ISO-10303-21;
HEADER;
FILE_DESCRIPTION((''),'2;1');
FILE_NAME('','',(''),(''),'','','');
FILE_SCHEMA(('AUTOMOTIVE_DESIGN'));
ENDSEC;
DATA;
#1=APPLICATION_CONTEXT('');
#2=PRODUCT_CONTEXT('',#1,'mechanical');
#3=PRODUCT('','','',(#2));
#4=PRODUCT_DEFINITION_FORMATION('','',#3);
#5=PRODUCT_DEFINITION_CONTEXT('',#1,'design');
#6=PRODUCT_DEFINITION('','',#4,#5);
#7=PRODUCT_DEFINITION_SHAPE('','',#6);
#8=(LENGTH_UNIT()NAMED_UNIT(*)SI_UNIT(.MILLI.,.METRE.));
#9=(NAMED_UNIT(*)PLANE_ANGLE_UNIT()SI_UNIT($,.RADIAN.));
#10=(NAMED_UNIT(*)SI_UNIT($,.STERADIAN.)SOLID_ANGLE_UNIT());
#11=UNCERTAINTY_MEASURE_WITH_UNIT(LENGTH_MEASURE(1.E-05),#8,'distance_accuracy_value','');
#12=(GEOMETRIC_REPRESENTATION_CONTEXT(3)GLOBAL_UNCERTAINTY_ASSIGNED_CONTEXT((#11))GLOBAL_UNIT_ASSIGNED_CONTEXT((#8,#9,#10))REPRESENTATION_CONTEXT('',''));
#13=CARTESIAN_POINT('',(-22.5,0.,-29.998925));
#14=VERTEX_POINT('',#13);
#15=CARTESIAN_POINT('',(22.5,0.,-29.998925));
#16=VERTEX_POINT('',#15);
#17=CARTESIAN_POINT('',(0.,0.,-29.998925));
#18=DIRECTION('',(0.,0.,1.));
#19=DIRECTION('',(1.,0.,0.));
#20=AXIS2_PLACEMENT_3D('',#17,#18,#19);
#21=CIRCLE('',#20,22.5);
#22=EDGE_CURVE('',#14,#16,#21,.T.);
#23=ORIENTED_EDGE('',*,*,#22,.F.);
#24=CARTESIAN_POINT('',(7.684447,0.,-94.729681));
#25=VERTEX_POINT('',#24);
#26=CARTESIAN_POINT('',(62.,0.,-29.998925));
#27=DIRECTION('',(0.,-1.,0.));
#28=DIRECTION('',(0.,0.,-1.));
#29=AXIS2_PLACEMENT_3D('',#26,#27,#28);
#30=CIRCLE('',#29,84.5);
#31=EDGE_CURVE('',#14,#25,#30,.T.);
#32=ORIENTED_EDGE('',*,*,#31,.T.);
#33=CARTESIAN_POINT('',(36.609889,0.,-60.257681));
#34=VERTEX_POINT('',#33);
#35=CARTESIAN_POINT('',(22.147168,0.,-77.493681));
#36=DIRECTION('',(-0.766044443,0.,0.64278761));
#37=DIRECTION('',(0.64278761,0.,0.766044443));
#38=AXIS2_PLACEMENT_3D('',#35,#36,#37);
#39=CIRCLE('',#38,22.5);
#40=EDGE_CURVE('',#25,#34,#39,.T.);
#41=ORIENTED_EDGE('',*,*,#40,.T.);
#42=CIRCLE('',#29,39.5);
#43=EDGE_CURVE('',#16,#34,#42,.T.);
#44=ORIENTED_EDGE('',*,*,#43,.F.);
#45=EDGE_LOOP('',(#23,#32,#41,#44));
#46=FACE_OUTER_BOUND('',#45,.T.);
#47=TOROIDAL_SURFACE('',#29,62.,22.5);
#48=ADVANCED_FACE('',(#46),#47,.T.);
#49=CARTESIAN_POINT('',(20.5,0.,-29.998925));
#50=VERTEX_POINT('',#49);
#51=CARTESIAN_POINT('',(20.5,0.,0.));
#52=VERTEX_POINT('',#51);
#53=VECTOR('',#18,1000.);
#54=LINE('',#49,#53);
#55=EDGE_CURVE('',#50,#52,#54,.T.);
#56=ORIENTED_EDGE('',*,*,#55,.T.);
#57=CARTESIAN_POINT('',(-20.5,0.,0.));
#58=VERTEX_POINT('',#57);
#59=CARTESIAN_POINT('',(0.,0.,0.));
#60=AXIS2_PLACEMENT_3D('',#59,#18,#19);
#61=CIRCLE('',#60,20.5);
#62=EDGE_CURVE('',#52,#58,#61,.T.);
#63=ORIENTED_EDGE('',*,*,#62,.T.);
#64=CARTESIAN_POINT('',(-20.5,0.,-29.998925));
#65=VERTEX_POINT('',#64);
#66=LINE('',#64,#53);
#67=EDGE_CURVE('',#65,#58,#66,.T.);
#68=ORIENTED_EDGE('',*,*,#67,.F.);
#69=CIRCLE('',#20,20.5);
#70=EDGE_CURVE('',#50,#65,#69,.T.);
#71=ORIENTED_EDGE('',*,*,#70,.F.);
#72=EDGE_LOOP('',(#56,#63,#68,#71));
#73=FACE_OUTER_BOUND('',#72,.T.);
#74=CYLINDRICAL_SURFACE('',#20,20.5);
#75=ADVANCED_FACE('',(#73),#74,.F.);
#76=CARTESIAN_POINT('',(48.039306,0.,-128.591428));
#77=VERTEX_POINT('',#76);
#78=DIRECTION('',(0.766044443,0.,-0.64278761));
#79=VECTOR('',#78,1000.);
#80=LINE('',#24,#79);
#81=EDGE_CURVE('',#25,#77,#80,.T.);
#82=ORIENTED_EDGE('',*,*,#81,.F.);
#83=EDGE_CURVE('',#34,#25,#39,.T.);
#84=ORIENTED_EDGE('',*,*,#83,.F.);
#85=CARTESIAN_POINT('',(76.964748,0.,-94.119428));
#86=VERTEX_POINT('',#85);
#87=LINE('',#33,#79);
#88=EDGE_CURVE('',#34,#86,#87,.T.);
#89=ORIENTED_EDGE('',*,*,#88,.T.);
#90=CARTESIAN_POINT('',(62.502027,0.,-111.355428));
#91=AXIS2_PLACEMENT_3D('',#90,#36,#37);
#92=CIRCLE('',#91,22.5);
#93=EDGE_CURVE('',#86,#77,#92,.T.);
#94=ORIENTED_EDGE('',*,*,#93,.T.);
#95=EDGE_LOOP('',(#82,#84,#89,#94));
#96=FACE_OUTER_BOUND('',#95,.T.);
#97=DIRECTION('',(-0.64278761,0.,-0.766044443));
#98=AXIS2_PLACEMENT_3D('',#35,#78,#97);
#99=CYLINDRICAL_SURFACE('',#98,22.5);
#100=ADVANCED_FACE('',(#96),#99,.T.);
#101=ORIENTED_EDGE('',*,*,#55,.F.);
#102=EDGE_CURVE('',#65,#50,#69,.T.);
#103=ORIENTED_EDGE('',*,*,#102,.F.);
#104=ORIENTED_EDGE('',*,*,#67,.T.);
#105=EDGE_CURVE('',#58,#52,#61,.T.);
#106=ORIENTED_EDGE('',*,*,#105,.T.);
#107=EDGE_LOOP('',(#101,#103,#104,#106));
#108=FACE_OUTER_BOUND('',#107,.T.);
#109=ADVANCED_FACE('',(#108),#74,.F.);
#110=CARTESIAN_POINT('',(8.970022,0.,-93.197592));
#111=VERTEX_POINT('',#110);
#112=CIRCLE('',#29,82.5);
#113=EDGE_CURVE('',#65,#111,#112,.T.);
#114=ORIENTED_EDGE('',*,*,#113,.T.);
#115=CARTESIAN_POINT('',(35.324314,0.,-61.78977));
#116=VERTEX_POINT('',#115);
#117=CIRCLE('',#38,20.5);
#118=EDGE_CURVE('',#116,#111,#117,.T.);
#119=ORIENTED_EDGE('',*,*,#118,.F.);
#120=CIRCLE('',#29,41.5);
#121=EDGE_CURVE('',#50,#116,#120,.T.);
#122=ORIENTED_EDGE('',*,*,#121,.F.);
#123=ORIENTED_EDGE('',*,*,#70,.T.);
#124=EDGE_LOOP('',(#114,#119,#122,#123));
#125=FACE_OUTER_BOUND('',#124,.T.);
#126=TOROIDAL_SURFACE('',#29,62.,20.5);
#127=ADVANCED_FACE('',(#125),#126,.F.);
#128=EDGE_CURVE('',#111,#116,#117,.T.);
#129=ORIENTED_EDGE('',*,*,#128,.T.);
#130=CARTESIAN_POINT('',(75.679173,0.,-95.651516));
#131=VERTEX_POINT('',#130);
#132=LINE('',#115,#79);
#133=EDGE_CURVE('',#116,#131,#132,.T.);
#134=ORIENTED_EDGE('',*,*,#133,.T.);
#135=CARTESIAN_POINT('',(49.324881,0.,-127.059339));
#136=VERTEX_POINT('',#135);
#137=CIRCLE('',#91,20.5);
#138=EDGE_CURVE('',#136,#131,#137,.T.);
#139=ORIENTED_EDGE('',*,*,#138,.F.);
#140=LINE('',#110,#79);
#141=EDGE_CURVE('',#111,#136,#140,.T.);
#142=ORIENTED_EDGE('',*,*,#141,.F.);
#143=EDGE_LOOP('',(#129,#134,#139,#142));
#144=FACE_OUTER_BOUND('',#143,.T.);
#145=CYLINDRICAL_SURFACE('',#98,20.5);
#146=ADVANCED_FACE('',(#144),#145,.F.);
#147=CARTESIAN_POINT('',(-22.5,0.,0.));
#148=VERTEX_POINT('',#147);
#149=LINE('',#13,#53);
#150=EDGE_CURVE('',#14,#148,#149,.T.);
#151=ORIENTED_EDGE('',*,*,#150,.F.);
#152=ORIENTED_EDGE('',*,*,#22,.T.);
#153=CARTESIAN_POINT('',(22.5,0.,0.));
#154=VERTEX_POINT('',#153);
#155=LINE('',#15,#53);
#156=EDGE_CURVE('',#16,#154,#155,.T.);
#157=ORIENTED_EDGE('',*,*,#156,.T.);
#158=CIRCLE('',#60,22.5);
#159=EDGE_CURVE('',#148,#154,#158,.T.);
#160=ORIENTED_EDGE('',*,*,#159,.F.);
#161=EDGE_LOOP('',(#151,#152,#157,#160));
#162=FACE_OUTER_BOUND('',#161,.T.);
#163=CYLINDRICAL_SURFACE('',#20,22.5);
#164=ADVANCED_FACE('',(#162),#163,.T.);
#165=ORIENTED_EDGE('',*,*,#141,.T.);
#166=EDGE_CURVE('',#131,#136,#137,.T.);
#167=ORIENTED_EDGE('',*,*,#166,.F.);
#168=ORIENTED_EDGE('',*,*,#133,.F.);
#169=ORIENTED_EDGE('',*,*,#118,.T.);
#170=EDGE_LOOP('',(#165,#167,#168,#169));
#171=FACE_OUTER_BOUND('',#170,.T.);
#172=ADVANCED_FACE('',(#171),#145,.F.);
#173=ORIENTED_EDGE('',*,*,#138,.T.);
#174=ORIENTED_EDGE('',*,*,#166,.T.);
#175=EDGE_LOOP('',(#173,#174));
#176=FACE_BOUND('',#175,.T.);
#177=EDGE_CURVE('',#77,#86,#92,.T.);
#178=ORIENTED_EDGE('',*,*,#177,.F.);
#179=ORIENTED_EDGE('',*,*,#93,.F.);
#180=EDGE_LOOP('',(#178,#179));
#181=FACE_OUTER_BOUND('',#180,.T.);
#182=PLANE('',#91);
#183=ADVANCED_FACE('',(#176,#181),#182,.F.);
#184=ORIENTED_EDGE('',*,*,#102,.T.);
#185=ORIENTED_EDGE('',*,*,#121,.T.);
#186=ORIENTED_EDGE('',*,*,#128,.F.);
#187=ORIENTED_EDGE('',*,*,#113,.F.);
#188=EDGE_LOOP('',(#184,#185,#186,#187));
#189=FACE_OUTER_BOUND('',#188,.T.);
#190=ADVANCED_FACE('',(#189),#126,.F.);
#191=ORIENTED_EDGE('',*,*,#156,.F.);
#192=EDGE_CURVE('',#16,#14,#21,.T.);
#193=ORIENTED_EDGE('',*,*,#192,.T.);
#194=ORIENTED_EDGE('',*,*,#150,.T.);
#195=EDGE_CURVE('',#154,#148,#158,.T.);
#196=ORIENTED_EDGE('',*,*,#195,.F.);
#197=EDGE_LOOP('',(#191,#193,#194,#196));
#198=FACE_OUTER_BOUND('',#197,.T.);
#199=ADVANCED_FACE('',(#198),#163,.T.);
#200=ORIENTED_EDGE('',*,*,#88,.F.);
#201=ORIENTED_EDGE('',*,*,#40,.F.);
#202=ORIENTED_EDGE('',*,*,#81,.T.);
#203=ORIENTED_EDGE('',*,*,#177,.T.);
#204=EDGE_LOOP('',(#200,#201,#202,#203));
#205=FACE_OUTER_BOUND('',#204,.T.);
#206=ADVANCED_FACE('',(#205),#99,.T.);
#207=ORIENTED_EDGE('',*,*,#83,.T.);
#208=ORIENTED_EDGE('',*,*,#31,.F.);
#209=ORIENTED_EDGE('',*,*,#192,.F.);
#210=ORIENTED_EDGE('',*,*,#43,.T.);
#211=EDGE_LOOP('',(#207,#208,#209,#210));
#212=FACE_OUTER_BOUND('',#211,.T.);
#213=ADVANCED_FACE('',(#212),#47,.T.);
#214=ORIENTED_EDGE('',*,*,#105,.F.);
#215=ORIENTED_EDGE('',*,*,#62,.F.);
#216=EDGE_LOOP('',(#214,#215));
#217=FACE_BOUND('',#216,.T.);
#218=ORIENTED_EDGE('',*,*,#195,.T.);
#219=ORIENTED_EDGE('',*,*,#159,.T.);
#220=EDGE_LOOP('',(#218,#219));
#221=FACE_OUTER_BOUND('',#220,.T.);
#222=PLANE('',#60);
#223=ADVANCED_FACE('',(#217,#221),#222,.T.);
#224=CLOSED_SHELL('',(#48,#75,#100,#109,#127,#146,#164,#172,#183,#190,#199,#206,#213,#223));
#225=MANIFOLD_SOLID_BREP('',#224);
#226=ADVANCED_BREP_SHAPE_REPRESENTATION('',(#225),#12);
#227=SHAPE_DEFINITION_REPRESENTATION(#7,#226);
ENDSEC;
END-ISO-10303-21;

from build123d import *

# Parameters (mm, degrees)
SKETCH1_R = 22.5
SHELL1_T  = -2


with BuildPart() as part:
    # Sweep1: sweep along a path in Sketch2
    with BuildLine(Plane(origin=(0, 0, 0), x_dir=(1, 0, 0), z_dir=(0, 1, 0))) as sweep1_path:
        Line((0, 0), (0, 29.998925194))
        ThreePointArc((0, 29.998925194), (5.808917204, 56.201257422), (22.147168199, 77.493680668))
        Line((22.147168199, 77.493680668), (62.502026728, 111.355427576))
    # Sketch1 → Sweep1 (sweep)
    with BuildSketch(Plane.XY):
        Circle(SKETCH1_R)
    sweep(path=sweep1_path.line)

    # Shell1
    shell1_openings = [part.faces().sort_by_distance(p)[0] for p in [
        (62.502026728, 0, -111.355427576),
        (0, 0, 0),
    ]]
    offset(amount=SHELL1_T, openings=shell1_openings, kind=Kind.INTERSECTION)


solid = part.part
